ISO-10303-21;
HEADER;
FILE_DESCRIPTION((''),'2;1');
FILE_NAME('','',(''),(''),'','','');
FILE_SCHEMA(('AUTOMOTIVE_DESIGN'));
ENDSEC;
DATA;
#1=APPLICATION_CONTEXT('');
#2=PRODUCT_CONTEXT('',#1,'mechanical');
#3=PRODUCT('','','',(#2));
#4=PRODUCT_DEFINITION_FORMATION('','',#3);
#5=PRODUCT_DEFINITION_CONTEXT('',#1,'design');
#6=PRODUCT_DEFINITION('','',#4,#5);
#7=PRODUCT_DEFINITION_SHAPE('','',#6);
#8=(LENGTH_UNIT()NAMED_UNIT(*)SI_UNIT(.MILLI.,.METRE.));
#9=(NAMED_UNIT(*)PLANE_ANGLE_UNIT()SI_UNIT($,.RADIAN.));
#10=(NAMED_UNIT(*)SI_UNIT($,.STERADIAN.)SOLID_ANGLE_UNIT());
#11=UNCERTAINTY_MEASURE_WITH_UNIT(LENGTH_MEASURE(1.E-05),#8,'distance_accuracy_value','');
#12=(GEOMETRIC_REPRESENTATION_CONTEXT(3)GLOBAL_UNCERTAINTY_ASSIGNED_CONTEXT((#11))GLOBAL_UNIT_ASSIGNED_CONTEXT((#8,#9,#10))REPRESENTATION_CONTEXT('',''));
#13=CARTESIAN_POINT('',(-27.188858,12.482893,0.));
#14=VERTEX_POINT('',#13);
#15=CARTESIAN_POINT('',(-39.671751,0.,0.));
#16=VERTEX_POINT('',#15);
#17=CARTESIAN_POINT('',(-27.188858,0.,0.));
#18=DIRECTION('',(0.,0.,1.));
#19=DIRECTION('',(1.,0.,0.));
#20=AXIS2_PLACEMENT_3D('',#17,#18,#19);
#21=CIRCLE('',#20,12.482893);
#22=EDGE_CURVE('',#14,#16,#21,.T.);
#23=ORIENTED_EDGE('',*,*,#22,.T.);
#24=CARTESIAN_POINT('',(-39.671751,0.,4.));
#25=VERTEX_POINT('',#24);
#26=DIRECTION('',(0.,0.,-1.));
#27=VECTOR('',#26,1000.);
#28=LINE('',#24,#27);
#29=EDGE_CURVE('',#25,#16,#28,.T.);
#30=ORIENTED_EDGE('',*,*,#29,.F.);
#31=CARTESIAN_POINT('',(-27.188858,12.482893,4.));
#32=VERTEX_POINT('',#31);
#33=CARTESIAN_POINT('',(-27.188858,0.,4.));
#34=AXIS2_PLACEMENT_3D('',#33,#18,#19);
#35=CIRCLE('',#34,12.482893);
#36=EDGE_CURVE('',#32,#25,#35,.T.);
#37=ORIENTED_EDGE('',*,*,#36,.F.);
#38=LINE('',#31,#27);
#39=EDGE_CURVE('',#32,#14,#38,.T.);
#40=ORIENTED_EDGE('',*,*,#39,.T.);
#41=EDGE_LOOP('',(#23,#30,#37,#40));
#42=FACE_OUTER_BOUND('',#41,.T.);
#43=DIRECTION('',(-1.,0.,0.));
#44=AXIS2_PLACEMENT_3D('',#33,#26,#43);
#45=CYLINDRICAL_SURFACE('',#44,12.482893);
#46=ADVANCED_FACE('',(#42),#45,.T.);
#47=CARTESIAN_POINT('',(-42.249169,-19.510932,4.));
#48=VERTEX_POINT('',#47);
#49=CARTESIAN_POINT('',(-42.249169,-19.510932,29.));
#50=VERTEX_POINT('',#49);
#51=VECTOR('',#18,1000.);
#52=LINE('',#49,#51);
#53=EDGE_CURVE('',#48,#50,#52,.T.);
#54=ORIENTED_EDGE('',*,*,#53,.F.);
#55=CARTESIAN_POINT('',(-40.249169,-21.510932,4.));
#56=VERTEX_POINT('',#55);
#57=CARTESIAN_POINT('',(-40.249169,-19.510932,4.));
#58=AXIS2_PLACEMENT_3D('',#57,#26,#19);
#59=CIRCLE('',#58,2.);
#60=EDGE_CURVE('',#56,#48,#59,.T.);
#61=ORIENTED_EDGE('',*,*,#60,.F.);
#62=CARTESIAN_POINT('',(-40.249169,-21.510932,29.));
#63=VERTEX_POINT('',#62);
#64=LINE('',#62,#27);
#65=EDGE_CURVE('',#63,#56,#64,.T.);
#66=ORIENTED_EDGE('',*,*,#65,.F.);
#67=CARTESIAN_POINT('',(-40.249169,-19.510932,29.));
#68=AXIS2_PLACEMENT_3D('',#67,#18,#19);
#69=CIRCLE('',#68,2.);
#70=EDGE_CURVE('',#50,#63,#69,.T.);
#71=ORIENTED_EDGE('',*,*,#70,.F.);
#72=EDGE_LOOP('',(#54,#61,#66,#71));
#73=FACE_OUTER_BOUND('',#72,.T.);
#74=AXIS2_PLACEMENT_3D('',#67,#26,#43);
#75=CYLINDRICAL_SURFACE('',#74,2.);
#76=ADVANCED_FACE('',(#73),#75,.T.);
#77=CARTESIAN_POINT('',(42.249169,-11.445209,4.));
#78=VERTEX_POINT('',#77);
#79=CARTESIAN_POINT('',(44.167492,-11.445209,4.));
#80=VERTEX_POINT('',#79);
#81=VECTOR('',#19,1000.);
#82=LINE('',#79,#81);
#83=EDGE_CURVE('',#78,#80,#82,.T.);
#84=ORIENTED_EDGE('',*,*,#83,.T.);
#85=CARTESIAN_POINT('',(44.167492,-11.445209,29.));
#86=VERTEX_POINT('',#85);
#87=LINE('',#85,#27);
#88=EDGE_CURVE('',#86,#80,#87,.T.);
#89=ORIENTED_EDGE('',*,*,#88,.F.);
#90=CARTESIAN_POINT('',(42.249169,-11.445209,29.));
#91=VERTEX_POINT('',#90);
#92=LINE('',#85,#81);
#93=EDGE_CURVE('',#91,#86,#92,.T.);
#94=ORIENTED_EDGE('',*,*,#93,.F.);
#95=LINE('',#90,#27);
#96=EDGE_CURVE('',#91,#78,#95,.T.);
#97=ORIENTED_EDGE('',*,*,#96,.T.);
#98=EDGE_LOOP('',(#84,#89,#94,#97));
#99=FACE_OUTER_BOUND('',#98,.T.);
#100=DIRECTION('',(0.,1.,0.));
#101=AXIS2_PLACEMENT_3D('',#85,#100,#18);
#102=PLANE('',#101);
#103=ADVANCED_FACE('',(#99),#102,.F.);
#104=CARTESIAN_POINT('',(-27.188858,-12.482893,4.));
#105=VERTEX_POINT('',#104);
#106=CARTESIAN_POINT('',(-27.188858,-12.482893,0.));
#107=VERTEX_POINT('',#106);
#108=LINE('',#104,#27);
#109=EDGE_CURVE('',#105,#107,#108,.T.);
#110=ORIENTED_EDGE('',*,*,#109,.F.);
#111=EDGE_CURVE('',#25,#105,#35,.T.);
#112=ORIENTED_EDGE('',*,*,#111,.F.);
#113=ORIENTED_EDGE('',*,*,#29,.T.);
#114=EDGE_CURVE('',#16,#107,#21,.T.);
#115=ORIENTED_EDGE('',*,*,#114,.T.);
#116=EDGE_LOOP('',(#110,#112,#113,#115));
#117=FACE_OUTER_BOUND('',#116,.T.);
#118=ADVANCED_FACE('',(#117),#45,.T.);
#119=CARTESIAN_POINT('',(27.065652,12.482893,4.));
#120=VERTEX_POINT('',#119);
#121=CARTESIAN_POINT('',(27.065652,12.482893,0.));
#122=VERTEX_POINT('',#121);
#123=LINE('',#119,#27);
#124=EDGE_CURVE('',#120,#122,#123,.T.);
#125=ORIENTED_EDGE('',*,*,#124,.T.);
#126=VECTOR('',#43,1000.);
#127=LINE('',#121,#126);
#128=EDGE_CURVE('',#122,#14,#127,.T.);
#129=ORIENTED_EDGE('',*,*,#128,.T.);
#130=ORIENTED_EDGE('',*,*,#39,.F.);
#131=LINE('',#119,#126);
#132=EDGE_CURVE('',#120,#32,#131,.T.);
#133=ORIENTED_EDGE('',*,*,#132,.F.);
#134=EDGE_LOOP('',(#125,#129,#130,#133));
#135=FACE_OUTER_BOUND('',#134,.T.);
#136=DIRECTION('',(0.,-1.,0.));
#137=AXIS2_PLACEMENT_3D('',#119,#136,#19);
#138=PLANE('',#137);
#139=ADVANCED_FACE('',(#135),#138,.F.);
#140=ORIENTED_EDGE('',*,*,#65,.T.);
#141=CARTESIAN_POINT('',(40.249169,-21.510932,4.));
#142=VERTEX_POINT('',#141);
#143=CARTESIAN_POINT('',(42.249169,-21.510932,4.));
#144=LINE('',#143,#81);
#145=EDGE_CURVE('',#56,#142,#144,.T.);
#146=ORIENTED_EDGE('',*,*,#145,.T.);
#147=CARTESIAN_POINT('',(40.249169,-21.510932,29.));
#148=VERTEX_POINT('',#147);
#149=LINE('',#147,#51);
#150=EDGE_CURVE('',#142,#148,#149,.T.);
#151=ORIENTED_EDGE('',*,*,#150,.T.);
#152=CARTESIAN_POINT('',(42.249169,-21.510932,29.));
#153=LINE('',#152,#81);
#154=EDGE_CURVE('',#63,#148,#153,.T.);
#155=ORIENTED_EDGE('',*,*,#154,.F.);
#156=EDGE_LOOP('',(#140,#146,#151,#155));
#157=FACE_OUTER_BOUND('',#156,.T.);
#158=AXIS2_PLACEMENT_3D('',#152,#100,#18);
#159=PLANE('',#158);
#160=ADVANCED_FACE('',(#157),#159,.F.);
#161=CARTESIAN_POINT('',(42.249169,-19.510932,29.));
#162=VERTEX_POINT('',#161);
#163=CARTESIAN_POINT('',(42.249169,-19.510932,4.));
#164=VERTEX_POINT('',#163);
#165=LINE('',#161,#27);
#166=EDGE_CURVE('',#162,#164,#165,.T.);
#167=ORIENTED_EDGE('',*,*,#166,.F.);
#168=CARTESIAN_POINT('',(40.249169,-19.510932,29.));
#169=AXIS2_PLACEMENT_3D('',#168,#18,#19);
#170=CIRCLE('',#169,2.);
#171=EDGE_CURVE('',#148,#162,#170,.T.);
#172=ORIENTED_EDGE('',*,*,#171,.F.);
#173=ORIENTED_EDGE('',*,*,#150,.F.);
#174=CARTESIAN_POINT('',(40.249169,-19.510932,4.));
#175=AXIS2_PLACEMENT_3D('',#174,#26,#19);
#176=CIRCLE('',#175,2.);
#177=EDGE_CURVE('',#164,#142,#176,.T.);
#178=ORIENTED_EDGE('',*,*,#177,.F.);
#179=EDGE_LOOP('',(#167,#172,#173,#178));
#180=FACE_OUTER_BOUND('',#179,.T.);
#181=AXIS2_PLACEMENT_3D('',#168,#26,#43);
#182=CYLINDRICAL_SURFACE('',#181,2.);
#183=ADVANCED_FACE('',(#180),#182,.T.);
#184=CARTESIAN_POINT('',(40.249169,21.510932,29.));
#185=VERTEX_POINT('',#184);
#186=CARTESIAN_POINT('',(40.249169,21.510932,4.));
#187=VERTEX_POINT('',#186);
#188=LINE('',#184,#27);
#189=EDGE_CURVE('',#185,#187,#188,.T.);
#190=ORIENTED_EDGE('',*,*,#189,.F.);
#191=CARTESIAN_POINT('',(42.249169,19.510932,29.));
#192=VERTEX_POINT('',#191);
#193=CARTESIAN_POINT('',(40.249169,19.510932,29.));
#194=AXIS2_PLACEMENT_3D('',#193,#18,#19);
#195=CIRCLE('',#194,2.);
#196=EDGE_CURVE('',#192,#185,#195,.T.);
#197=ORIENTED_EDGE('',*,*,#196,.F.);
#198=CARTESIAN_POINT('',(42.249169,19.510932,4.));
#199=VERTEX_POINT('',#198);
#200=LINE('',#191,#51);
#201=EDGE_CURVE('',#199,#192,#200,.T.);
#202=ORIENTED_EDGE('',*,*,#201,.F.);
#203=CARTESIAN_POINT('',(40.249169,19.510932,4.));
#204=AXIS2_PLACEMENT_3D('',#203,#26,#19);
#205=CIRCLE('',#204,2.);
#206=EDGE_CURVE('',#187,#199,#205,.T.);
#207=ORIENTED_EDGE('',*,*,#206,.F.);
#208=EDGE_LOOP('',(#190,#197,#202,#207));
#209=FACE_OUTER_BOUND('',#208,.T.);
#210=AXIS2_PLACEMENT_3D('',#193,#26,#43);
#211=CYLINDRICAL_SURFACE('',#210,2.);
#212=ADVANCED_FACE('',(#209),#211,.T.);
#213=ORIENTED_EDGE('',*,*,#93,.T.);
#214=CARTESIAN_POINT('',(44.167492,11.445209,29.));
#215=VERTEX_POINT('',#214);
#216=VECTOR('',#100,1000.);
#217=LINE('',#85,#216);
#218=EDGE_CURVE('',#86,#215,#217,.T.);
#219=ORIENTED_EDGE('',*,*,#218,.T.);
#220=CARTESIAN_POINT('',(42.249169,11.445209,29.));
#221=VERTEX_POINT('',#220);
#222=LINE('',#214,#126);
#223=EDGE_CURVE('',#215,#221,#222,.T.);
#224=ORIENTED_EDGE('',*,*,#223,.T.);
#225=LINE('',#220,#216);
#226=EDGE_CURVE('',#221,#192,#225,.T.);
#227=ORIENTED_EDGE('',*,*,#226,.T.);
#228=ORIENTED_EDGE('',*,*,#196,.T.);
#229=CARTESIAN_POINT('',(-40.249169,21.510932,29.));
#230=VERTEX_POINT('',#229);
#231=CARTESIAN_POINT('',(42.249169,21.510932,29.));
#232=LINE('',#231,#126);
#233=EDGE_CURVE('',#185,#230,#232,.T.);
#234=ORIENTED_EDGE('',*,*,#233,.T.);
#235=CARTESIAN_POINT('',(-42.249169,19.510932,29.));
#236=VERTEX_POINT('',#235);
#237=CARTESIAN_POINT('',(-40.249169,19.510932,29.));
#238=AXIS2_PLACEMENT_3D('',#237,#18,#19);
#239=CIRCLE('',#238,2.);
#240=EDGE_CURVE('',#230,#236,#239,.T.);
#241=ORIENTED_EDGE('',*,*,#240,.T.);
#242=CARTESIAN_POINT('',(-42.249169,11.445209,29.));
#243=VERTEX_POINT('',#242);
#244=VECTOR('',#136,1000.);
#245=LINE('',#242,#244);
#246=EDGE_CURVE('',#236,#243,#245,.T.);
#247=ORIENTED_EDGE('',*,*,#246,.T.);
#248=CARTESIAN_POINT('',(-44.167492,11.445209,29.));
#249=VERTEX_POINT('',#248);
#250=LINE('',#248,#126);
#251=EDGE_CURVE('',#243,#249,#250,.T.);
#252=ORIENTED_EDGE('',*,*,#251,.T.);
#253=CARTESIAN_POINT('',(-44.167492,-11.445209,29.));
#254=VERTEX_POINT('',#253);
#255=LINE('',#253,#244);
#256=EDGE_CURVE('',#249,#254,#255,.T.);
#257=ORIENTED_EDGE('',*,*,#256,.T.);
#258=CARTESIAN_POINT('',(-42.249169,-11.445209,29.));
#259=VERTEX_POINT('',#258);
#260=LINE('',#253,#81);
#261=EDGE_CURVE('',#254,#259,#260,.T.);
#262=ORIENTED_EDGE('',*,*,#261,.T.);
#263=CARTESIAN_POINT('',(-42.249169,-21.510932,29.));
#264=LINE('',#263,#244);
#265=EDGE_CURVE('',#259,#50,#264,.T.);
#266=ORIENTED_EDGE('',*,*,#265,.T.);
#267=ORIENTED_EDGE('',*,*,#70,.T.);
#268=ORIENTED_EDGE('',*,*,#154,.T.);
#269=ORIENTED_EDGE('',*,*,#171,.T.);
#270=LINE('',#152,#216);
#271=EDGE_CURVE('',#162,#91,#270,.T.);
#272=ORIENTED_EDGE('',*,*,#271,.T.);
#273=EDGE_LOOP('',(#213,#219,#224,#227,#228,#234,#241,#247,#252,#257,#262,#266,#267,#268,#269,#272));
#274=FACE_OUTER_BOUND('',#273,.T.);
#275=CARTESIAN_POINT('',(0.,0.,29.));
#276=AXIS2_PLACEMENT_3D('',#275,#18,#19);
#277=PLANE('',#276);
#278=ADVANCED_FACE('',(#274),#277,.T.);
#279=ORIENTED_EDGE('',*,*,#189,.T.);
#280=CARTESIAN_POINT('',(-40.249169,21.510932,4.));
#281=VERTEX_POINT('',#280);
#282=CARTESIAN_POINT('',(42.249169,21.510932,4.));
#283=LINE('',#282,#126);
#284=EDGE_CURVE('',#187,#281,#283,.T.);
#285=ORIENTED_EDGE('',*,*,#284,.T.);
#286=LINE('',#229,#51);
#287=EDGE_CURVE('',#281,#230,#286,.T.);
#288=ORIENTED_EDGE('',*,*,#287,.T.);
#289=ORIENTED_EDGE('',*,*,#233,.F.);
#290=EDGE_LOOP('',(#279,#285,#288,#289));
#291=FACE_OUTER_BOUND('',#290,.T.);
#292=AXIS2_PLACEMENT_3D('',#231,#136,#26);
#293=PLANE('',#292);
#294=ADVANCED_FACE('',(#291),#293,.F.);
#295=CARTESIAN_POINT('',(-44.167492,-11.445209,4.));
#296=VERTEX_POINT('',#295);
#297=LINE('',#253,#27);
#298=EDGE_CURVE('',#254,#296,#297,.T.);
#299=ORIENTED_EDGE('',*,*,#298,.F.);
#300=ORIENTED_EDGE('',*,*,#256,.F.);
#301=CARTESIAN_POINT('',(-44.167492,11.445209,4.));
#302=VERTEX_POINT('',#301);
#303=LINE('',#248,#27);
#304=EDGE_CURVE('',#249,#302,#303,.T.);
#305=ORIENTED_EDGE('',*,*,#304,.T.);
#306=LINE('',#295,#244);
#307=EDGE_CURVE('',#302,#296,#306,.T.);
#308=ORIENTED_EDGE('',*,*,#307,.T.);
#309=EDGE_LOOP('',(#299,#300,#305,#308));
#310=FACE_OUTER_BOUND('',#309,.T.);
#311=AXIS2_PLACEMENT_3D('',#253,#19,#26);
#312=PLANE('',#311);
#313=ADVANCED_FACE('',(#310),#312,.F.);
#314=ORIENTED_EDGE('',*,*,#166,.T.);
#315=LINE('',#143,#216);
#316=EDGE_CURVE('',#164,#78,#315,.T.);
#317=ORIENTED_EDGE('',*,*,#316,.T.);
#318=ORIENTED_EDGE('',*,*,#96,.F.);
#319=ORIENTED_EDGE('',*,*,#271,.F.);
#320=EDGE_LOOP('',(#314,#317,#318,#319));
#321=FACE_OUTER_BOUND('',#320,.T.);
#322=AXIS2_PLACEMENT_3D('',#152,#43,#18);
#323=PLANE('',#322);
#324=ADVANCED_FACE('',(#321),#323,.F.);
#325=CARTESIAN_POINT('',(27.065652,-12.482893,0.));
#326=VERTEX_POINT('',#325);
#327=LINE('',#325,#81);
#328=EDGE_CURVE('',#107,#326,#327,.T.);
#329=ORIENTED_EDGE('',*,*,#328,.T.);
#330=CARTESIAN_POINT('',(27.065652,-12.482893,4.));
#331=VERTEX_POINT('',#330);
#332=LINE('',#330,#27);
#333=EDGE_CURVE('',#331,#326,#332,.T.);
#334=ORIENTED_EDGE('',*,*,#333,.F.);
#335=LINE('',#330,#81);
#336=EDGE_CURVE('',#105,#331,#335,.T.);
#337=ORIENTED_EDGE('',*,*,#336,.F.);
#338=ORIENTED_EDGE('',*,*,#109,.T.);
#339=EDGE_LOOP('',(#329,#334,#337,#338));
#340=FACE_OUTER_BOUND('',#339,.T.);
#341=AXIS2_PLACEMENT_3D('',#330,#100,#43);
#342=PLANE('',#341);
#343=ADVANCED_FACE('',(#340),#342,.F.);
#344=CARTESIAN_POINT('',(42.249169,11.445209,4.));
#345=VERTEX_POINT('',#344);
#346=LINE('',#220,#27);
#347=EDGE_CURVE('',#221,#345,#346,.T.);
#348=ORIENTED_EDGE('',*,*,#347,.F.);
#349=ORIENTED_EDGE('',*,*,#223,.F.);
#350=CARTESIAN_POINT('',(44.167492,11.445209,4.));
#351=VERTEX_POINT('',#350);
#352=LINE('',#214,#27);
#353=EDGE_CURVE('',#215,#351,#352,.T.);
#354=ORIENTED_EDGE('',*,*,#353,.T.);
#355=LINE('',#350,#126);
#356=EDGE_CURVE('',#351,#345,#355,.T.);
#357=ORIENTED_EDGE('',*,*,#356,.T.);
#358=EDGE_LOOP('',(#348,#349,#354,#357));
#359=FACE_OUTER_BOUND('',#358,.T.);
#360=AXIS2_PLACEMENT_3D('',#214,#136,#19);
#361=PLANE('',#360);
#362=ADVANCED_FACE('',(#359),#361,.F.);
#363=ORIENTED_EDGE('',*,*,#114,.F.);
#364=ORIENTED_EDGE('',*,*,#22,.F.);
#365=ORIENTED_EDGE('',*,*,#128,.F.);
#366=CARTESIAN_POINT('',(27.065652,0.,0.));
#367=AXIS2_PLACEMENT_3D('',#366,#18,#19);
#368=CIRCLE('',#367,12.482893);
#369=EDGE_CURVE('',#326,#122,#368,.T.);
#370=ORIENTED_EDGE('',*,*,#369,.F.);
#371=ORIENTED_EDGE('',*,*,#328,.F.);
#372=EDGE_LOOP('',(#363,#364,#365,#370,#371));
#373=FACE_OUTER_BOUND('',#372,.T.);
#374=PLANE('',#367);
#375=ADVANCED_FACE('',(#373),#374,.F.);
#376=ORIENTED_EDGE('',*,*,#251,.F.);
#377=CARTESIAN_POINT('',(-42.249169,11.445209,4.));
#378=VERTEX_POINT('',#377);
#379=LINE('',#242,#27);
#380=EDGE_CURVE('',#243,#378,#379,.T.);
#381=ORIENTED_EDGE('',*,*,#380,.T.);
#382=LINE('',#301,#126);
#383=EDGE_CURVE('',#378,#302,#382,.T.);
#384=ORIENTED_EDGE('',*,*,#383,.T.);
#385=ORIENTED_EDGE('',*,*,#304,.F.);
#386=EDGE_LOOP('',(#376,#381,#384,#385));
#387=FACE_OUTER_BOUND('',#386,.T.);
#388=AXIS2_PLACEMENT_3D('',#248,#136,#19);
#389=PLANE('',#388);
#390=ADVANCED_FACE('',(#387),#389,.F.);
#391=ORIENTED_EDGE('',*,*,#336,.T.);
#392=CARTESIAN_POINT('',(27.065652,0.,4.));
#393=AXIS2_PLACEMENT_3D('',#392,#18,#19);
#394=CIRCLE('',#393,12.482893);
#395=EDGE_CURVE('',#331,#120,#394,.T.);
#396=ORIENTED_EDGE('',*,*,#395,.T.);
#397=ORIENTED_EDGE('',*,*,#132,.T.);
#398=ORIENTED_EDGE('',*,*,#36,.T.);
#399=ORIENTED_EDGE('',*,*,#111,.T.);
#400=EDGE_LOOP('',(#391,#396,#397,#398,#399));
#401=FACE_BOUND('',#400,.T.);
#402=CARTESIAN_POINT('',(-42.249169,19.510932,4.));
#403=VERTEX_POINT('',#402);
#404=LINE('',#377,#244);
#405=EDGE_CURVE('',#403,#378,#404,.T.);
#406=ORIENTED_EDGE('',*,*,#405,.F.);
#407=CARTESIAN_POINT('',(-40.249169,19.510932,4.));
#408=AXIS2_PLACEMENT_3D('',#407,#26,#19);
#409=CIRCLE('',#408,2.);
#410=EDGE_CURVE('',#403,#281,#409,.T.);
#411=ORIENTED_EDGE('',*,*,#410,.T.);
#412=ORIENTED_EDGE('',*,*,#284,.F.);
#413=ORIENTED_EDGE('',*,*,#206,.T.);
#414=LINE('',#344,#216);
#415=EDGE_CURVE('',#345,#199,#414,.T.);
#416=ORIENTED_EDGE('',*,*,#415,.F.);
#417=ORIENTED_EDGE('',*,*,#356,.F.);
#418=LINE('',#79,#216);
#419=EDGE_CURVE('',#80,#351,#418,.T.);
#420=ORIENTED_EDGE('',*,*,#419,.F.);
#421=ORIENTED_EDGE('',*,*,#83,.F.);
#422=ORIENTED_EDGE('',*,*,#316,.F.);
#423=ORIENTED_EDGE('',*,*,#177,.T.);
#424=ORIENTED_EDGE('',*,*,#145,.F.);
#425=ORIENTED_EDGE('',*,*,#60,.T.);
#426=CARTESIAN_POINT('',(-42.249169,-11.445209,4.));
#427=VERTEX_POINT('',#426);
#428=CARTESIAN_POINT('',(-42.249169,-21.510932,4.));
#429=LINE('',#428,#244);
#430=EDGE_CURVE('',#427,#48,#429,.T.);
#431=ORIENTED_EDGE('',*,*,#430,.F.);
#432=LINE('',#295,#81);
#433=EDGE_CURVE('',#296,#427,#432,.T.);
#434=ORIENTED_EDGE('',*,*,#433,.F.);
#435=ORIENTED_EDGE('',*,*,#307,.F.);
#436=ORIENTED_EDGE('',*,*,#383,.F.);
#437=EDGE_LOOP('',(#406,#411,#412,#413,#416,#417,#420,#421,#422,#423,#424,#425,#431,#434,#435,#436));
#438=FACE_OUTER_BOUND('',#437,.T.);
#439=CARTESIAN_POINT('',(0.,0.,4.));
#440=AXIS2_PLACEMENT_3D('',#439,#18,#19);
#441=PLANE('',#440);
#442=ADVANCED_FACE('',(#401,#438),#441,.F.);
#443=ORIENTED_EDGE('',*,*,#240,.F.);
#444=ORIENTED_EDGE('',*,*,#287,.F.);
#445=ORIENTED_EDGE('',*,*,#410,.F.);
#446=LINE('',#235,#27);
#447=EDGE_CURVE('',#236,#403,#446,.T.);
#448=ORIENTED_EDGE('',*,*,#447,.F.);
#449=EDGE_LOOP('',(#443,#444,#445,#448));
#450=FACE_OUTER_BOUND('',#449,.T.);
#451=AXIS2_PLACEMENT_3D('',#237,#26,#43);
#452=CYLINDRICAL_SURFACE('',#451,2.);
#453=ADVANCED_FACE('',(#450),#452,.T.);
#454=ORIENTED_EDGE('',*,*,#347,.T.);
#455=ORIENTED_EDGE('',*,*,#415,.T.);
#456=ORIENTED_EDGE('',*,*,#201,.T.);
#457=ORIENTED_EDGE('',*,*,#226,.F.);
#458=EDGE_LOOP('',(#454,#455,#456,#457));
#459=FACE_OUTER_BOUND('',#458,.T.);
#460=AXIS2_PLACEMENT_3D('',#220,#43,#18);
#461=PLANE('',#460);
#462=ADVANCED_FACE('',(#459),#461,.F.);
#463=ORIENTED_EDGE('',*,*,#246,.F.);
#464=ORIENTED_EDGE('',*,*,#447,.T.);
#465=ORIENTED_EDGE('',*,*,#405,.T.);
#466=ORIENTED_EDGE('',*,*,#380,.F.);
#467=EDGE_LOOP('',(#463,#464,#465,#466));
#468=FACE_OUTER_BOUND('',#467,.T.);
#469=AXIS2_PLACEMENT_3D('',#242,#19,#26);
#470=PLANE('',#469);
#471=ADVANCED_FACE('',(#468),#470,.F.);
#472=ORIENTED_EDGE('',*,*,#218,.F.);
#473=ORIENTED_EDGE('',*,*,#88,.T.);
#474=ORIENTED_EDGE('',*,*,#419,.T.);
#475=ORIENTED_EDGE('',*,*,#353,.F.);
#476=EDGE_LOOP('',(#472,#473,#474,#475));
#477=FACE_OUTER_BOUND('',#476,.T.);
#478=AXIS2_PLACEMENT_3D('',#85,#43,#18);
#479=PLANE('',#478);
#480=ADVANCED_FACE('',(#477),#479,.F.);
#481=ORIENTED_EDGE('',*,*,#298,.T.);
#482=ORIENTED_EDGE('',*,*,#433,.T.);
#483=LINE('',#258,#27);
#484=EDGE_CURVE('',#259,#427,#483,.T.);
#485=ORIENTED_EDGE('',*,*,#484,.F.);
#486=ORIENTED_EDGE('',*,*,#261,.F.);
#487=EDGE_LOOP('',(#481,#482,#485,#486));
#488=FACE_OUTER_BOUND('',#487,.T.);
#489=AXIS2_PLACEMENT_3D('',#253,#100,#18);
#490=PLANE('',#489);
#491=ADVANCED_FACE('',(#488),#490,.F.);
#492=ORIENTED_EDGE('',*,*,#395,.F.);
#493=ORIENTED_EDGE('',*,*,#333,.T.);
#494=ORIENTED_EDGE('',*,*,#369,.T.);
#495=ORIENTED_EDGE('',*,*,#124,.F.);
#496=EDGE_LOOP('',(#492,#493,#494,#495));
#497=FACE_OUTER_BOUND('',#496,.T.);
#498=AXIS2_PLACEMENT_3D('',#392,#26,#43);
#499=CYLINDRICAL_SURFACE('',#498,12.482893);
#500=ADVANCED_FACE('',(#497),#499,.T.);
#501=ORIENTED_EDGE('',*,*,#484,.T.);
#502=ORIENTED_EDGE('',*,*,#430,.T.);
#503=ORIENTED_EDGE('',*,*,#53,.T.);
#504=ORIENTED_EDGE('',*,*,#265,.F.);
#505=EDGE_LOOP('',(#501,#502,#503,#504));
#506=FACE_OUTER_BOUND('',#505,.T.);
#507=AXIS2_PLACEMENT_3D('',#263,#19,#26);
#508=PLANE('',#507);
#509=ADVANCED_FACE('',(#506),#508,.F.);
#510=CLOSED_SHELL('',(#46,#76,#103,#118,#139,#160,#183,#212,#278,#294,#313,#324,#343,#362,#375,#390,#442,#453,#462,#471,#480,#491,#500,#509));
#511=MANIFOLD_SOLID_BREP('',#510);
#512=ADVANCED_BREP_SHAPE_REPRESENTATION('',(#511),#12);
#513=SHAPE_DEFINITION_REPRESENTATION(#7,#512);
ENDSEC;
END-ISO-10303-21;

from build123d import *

# Parameters (mm, degrees)
BOSS_EXTRUDE1_DEPTH = 4
BOSS_EXTRUDE2_DEPTH = 25
FILLET1_R           = 2


with BuildPart() as part:
    # Sketch1 → Boss-Extrude1 (new body)
    with BuildSketch(Plane.XY):
        with BuildLine():
            Line((27.065651732, -12.482893197), (-27.188857752, -12.482893197))
            ThreePointArc((-27.188857752, -12.482893197), (-39.671750949, 0), (-27.188857752, 12.482893197))
            Line((-27.188857752, 12.482893197), (27.065651732, 12.482893197))
            ThreePointArc((27.065651732, 12.482893197), (39.548544929, 0), (27.065651732, -12.482893197))
        make_face()
    extrude(amount=BOSS_EXTRUDE1_DEPTH)

    # Sketch2 → Boss-Extrude2 (add)
    with BuildSketch(Plane.XY.offset(4)):
        Polygon((42.249168755, -21.510932303), (-42.249168755, -21.510932303), (-42.249168755, -11.445209118), (-44.167491565, -11.445209118), (-44.167491565, 11.445209118), (-42.249168755, 11.445209118), (-42.249168755, 21.510932303), (42.249168755, 21.510932303), (42.249168755, 11.445209118), (44.167491565, 11.445209118), (44.167491565, -11.445209118), (42.249168755, -11.445209118), align=None)
    extrude(amount=BOSS_EXTRUDE2_DEPTH)

    # Fillet1
    fillet1_edges = [part.edges().sort_by_distance(p)[0] for p in [
        (-42.249168755, 21.510932303, 16.5),
        (-42.249168755, -21.510932303, 16.5),
        (42.249168755, -21.510932303, 16.5),
        (42.249168755, 21.510932303, 16.5),
    ]]
    fillet(fillet1_edges, radius=FILLET1_R)


solid = part.part
